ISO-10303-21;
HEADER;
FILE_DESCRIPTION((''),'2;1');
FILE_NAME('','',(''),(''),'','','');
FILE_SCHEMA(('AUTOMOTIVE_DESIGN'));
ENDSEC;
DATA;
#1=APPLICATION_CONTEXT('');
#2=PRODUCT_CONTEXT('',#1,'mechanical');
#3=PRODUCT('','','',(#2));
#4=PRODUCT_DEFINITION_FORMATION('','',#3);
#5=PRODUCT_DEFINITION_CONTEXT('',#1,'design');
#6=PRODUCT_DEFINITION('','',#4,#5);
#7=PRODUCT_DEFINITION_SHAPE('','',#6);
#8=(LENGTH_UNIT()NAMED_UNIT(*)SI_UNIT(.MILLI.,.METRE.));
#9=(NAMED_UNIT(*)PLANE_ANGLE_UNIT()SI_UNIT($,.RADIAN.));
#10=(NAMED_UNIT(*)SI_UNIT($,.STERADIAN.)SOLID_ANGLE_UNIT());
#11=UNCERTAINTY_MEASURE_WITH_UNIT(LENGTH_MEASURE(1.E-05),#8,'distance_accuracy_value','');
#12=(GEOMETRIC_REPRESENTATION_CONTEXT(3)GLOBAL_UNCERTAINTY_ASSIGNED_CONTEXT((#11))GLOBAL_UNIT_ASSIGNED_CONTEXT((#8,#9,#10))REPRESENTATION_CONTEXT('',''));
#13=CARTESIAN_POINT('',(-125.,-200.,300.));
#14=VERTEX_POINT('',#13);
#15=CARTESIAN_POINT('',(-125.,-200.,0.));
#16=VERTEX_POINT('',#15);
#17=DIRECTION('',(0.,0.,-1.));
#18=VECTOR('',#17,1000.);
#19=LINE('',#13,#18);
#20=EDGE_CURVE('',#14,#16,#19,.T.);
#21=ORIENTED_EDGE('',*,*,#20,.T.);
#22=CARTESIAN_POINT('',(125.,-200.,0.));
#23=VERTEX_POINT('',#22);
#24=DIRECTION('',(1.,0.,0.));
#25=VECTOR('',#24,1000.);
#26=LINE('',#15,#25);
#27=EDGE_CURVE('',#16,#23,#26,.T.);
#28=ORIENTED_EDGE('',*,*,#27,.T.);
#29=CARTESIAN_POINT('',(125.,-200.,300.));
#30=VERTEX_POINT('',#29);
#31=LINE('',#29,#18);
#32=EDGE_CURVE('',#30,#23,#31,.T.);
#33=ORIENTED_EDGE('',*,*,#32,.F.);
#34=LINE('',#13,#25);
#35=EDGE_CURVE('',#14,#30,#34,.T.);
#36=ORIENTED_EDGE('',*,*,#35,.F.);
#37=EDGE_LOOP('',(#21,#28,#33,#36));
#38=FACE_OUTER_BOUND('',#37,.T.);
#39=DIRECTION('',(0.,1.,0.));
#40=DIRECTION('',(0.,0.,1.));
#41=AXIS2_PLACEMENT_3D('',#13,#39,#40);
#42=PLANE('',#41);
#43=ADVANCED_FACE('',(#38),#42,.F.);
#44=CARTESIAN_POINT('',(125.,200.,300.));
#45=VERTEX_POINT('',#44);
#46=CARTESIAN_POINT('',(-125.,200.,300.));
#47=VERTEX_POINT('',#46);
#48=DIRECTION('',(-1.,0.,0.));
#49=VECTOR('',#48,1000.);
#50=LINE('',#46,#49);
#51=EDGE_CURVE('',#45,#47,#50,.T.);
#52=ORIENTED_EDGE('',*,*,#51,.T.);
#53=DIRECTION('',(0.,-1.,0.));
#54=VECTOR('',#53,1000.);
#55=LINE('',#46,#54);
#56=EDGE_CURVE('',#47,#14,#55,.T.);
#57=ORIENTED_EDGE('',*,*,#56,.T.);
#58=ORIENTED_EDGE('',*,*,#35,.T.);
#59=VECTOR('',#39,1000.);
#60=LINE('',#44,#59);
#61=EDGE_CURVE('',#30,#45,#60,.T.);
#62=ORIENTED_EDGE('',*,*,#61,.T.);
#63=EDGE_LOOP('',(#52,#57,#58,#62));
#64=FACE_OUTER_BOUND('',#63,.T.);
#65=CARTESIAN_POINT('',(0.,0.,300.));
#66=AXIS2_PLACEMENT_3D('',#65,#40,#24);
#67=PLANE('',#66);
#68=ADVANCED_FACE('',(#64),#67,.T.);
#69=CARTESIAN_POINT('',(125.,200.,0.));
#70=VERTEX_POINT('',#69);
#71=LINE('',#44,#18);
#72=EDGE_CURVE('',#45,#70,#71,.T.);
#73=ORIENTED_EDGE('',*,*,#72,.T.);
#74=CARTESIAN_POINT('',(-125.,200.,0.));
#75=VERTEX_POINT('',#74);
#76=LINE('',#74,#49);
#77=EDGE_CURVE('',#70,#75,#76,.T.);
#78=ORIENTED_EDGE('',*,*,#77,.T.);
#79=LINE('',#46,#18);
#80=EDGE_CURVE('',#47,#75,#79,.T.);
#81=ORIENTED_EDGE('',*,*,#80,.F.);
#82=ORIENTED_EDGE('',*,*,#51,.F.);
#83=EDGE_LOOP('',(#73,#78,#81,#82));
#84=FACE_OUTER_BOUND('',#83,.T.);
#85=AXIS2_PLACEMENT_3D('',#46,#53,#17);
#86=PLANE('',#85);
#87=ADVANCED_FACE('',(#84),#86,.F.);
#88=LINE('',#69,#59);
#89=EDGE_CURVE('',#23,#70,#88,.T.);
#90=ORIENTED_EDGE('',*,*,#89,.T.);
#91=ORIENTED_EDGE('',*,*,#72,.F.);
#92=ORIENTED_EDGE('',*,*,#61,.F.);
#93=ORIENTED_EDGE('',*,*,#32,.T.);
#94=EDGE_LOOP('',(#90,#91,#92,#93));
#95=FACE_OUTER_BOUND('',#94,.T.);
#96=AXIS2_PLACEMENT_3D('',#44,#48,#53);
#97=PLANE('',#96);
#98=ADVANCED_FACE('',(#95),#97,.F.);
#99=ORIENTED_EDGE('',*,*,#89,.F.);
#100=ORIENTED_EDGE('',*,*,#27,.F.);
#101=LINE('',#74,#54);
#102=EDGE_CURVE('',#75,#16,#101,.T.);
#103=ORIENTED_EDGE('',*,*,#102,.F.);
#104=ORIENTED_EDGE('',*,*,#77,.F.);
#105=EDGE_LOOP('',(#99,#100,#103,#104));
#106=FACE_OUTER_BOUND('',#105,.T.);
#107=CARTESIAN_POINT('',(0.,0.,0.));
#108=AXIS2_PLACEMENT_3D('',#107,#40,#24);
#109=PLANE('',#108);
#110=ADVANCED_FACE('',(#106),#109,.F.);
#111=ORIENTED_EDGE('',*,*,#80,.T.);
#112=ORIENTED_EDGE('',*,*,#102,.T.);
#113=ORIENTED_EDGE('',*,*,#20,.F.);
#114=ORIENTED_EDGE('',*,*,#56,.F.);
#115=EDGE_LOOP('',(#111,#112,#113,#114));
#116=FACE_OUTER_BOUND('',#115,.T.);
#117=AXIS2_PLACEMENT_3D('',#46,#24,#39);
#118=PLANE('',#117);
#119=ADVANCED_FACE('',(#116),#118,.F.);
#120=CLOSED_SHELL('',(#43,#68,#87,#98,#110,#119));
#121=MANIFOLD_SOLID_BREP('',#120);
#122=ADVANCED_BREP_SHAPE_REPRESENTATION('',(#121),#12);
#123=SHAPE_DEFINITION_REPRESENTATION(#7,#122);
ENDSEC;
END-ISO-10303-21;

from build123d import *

# Parameters (mm, degrees)
SKETCH1_W           = 250
SKETCH1_H           = 400
BOSS_EXTRUDE1_DEPTH = 300


with BuildPart() as part:
    # Sketch1 → Boss-Extrude1 (new body)
    with BuildSketch(Plane.XY):
        Rectangle(SKETCH1_W, SKETCH1_H)
    extrude(amount=BOSS_EXTRUDE1_DEPTH)


solid = part.part
